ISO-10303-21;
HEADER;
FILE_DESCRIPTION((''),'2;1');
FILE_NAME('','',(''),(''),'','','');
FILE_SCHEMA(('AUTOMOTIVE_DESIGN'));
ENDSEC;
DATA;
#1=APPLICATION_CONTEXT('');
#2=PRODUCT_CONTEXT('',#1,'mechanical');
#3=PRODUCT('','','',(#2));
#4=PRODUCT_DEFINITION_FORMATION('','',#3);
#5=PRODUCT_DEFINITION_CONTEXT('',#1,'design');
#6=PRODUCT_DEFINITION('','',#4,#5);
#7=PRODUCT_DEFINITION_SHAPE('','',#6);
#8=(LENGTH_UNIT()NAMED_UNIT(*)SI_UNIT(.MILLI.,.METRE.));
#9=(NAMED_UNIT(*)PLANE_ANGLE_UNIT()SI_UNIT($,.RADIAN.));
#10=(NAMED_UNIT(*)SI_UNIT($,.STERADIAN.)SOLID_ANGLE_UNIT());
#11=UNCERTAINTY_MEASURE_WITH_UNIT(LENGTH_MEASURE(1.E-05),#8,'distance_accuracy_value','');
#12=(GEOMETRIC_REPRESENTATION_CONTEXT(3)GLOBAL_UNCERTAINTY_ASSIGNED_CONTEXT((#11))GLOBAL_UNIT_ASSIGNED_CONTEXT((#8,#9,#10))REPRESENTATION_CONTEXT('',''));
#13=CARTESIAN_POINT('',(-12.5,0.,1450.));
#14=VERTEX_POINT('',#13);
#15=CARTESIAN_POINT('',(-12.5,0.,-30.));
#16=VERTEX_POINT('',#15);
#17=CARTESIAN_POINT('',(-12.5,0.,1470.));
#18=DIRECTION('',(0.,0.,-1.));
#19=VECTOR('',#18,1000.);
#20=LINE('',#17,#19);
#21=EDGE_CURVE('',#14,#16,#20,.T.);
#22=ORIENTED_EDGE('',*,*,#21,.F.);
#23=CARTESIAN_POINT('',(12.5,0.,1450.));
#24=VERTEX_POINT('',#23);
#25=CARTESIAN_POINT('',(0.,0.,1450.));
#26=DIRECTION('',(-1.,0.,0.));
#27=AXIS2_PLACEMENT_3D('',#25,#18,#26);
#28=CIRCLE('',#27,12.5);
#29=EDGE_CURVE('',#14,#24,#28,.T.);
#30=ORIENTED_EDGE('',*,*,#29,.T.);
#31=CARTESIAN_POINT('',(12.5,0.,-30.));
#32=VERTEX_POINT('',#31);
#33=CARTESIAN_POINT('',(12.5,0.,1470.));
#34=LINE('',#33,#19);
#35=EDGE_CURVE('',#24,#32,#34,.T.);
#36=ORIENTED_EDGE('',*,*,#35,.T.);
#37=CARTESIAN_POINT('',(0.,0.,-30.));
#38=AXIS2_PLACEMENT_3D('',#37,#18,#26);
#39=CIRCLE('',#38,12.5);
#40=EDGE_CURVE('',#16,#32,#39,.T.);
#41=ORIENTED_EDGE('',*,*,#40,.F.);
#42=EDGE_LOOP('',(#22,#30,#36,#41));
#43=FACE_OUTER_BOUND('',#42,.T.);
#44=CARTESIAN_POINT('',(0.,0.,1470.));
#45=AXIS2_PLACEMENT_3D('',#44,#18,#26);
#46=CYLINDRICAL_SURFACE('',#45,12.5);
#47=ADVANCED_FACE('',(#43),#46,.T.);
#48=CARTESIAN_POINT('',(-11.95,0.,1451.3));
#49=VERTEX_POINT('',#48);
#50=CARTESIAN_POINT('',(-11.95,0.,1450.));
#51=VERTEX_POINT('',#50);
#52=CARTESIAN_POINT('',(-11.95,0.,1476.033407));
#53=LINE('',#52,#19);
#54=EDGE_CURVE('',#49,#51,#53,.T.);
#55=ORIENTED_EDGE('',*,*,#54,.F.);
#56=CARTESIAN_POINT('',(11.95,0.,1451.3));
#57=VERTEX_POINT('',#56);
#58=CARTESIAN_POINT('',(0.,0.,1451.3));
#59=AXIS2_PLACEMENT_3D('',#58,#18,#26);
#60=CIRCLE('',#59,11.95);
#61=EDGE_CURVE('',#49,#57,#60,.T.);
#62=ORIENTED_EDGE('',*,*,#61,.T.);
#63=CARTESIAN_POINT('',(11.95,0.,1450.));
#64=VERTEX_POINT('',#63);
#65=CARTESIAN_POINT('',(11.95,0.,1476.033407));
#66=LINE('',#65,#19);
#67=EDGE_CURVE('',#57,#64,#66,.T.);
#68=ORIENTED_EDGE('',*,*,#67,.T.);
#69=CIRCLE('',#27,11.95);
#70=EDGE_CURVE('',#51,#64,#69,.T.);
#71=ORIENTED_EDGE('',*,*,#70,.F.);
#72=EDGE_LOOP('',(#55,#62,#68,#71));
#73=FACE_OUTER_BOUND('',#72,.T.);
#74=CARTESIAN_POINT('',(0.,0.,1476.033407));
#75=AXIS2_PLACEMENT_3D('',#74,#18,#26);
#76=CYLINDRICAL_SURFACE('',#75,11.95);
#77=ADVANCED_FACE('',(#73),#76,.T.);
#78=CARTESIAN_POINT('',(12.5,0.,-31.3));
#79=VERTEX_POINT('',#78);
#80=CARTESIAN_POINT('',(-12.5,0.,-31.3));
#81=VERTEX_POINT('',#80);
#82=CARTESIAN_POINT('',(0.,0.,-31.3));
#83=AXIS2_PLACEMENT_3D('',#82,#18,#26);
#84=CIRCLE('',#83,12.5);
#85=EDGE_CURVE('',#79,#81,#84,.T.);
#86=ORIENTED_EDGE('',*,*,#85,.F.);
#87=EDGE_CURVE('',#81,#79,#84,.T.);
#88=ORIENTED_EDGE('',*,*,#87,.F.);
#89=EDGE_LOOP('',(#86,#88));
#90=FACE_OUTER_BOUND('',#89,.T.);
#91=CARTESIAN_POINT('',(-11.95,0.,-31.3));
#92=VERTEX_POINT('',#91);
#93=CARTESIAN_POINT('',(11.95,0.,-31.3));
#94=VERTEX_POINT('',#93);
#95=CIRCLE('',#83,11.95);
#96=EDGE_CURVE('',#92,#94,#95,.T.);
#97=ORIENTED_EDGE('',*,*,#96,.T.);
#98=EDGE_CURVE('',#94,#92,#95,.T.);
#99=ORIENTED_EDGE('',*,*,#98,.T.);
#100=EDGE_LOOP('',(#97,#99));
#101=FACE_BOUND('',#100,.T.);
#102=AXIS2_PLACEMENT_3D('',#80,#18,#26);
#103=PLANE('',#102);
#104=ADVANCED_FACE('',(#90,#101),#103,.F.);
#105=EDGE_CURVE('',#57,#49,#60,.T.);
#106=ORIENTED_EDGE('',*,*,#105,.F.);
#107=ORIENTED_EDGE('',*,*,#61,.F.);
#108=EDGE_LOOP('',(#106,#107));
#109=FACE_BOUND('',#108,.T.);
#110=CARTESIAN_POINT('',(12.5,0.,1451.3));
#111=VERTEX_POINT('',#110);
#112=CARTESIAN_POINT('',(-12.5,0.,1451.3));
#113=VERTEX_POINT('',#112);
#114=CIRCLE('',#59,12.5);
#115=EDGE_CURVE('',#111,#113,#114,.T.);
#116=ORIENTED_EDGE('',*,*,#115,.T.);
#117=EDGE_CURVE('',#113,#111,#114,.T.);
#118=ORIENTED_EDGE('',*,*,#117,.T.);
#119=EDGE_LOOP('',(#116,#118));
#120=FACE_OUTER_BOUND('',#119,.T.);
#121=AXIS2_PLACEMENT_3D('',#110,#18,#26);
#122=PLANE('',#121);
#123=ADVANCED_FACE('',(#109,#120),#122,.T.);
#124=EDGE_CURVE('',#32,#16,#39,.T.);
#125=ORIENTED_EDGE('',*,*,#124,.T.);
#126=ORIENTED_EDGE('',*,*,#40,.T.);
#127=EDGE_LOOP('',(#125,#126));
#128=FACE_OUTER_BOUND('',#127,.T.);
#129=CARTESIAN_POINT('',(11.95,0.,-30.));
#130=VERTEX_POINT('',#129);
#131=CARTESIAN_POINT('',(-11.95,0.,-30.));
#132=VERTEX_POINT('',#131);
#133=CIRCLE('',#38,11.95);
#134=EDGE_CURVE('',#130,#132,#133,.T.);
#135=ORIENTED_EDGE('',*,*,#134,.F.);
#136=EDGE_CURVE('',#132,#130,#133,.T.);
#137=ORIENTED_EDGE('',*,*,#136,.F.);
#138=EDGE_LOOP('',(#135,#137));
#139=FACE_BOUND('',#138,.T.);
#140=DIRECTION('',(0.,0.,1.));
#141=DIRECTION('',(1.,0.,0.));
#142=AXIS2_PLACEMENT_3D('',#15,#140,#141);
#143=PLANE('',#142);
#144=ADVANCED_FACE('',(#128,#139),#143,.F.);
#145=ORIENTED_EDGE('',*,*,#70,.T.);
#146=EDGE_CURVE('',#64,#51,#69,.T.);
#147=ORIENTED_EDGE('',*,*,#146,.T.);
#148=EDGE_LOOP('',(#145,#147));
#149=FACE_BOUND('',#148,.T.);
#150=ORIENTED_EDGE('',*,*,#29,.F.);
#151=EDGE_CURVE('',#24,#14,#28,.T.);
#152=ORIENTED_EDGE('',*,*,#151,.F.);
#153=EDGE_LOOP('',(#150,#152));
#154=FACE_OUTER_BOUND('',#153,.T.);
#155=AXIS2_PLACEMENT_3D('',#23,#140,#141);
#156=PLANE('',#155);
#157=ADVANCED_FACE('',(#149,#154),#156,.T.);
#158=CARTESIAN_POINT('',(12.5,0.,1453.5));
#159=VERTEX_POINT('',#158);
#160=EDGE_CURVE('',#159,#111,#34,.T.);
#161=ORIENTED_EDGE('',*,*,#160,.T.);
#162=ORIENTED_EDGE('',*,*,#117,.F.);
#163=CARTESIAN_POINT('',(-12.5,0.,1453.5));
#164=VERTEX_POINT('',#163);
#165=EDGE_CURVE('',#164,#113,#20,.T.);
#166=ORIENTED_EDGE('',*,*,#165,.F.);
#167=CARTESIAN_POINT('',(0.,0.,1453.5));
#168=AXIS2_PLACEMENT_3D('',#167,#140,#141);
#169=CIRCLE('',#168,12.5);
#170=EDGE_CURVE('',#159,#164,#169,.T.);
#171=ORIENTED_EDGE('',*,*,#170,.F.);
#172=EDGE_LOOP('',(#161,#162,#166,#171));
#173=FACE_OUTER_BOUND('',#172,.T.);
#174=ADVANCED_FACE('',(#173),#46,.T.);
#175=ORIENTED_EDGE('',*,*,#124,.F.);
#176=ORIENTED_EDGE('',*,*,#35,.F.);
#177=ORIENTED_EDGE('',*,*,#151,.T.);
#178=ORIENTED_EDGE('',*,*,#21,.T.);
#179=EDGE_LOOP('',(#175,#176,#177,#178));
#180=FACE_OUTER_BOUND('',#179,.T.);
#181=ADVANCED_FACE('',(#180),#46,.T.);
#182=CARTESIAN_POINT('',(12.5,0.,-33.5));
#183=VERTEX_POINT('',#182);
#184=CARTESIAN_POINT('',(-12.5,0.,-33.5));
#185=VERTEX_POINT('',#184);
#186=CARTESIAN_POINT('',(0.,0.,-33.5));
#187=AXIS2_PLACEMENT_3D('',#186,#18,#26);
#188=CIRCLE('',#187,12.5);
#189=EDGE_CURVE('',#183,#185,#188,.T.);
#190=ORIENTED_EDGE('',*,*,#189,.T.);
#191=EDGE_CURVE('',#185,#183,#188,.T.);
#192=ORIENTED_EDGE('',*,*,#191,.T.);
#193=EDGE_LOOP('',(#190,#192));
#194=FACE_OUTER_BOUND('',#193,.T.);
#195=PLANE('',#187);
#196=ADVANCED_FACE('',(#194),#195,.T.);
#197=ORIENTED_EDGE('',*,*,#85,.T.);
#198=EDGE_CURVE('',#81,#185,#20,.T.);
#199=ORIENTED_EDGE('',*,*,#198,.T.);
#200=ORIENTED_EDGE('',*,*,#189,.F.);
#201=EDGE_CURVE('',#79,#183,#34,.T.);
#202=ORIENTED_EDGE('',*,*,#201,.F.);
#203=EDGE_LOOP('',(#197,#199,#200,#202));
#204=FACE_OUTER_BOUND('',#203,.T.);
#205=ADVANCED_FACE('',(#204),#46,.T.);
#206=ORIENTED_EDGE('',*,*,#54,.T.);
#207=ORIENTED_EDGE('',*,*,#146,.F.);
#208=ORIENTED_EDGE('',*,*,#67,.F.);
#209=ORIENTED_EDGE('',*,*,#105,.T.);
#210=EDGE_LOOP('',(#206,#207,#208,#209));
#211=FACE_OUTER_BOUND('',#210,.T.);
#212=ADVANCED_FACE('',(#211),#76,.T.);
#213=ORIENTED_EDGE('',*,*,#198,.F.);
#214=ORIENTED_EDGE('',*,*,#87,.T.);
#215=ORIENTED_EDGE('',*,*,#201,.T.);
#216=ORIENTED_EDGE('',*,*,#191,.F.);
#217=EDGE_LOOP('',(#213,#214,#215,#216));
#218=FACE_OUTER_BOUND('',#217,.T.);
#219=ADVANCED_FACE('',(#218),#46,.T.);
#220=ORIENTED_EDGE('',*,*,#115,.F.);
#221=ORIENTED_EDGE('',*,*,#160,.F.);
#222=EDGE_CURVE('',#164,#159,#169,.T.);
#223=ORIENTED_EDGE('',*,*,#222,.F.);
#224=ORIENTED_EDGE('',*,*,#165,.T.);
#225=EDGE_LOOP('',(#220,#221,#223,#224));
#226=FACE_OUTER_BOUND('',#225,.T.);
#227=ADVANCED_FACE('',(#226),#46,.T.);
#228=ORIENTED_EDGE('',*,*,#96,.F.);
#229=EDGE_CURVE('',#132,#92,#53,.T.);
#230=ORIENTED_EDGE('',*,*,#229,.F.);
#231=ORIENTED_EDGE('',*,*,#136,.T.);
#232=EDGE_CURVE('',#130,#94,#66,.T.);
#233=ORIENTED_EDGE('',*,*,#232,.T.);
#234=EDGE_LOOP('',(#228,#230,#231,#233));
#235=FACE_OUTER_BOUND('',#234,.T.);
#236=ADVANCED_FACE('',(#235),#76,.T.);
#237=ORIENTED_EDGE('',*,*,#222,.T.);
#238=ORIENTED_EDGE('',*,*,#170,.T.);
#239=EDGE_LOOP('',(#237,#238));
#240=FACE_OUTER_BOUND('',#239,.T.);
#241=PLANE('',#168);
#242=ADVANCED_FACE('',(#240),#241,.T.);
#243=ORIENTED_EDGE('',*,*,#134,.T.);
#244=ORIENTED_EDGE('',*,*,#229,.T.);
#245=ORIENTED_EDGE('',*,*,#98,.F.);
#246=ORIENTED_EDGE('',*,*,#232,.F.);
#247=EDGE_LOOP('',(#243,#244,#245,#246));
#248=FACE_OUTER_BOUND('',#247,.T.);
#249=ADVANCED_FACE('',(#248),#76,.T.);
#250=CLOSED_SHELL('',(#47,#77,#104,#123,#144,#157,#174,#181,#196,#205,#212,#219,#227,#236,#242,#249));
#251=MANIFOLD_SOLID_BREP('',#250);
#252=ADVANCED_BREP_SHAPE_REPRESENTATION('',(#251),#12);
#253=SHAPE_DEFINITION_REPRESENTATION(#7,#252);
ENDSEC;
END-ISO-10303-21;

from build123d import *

# Parameters (mm, degrees)
SKETCH_1_R          = 12.5
EXTRUDE_1_DEPTH     = 1470
EXTRUDE_START       = 50
SKETCH_9_R          = 12.5
EXTRUDE_5_DEPTH     = 50
SKETCH_2_W          = 0.55
SKETCH_2_H          = 1.3
CUT_EXTRUDE_START   = -16.5
SKETCH_11_R         = 12.5
CUT_EXTRUDE_2_DEPTH = 16.5
SKETCH_12_R         = 12.5
CUT_EXTRUDE_3_DEPTH = 16.5


with BuildPart() as part:
    # 草图1 → 凸台-拉伸1 (new body)
    with BuildSketch(Plane.XY):
        Circle(SKETCH_1_R)
    extrude(amount=EXTRUDE_1_DEPTH)

    # 草图9 → 凸台-拉伸5 (add)
    with BuildSketch(Plane(origin=(0, 0, 0), x_dir=(-1, 0, 0), z_dir=(0, 0, -1)).offset(EXTRUDE_START)):
        Circle(SKETCH_9_R)
    extrude(amount=-EXTRUDE_5_DEPTH)

    # 草图2 → 切除-旋转1 (revolve, cut)
    with BuildSketch(Plane(origin=(0, 0, 0), x_dir=(1, 0, 0), z_dir=(0, 1, 0)), mode=Mode.PRIVATE) as cut_revolve_1_sk:
        with Locations((12.225, -1450.65)):
            Rectangle(SKETCH_2_W, SKETCH_2_H)
        with Locations((-12.225, -1450.65)):
            Rectangle(SKETCH_2_W, SKETCH_2_H)
        with Locations((-12.225, 30.65)):
            Rectangle(SKETCH_2_W, SKETCH_2_H)
        with Locations((12.225, 30.65)):
            Rectangle(SKETCH_2_W, SKETCH_2_H)
    revolve(cut_revolve_1_sk.sketch.rotate(Axis((0, 0, 1476.033406801), (0, 0, 1)), 180), axis=Axis((0, 0, 1476.033406801), (0, 0, 1)), mode=Mode.SUBTRACT)

    # 草图11 → 切除-拉伸2 (cut)
    with BuildSketch(Plane.XY.offset(1470).offset(CUT_EXTRUDE_START)):
        with Locations(Location((0, 0, 0), (0, 0, 180))):
            Circle(SKETCH_11_R)
    extrude(amount=CUT_EXTRUDE_2_DEPTH, mode=Mode.SUBTRACT)

    # 草图12 → 切除-拉伸3 (cut)
    with BuildSketch(Plane(origin=(0, 0, -50), x_dir=(-1, 0, 0), z_dir=(0, 0, -1))):
        Circle(SKETCH_12_R)
    extrude(amount=-CUT_EXTRUDE_3_DEPTH, mode=Mode.SUBTRACT)


solid = part.part
